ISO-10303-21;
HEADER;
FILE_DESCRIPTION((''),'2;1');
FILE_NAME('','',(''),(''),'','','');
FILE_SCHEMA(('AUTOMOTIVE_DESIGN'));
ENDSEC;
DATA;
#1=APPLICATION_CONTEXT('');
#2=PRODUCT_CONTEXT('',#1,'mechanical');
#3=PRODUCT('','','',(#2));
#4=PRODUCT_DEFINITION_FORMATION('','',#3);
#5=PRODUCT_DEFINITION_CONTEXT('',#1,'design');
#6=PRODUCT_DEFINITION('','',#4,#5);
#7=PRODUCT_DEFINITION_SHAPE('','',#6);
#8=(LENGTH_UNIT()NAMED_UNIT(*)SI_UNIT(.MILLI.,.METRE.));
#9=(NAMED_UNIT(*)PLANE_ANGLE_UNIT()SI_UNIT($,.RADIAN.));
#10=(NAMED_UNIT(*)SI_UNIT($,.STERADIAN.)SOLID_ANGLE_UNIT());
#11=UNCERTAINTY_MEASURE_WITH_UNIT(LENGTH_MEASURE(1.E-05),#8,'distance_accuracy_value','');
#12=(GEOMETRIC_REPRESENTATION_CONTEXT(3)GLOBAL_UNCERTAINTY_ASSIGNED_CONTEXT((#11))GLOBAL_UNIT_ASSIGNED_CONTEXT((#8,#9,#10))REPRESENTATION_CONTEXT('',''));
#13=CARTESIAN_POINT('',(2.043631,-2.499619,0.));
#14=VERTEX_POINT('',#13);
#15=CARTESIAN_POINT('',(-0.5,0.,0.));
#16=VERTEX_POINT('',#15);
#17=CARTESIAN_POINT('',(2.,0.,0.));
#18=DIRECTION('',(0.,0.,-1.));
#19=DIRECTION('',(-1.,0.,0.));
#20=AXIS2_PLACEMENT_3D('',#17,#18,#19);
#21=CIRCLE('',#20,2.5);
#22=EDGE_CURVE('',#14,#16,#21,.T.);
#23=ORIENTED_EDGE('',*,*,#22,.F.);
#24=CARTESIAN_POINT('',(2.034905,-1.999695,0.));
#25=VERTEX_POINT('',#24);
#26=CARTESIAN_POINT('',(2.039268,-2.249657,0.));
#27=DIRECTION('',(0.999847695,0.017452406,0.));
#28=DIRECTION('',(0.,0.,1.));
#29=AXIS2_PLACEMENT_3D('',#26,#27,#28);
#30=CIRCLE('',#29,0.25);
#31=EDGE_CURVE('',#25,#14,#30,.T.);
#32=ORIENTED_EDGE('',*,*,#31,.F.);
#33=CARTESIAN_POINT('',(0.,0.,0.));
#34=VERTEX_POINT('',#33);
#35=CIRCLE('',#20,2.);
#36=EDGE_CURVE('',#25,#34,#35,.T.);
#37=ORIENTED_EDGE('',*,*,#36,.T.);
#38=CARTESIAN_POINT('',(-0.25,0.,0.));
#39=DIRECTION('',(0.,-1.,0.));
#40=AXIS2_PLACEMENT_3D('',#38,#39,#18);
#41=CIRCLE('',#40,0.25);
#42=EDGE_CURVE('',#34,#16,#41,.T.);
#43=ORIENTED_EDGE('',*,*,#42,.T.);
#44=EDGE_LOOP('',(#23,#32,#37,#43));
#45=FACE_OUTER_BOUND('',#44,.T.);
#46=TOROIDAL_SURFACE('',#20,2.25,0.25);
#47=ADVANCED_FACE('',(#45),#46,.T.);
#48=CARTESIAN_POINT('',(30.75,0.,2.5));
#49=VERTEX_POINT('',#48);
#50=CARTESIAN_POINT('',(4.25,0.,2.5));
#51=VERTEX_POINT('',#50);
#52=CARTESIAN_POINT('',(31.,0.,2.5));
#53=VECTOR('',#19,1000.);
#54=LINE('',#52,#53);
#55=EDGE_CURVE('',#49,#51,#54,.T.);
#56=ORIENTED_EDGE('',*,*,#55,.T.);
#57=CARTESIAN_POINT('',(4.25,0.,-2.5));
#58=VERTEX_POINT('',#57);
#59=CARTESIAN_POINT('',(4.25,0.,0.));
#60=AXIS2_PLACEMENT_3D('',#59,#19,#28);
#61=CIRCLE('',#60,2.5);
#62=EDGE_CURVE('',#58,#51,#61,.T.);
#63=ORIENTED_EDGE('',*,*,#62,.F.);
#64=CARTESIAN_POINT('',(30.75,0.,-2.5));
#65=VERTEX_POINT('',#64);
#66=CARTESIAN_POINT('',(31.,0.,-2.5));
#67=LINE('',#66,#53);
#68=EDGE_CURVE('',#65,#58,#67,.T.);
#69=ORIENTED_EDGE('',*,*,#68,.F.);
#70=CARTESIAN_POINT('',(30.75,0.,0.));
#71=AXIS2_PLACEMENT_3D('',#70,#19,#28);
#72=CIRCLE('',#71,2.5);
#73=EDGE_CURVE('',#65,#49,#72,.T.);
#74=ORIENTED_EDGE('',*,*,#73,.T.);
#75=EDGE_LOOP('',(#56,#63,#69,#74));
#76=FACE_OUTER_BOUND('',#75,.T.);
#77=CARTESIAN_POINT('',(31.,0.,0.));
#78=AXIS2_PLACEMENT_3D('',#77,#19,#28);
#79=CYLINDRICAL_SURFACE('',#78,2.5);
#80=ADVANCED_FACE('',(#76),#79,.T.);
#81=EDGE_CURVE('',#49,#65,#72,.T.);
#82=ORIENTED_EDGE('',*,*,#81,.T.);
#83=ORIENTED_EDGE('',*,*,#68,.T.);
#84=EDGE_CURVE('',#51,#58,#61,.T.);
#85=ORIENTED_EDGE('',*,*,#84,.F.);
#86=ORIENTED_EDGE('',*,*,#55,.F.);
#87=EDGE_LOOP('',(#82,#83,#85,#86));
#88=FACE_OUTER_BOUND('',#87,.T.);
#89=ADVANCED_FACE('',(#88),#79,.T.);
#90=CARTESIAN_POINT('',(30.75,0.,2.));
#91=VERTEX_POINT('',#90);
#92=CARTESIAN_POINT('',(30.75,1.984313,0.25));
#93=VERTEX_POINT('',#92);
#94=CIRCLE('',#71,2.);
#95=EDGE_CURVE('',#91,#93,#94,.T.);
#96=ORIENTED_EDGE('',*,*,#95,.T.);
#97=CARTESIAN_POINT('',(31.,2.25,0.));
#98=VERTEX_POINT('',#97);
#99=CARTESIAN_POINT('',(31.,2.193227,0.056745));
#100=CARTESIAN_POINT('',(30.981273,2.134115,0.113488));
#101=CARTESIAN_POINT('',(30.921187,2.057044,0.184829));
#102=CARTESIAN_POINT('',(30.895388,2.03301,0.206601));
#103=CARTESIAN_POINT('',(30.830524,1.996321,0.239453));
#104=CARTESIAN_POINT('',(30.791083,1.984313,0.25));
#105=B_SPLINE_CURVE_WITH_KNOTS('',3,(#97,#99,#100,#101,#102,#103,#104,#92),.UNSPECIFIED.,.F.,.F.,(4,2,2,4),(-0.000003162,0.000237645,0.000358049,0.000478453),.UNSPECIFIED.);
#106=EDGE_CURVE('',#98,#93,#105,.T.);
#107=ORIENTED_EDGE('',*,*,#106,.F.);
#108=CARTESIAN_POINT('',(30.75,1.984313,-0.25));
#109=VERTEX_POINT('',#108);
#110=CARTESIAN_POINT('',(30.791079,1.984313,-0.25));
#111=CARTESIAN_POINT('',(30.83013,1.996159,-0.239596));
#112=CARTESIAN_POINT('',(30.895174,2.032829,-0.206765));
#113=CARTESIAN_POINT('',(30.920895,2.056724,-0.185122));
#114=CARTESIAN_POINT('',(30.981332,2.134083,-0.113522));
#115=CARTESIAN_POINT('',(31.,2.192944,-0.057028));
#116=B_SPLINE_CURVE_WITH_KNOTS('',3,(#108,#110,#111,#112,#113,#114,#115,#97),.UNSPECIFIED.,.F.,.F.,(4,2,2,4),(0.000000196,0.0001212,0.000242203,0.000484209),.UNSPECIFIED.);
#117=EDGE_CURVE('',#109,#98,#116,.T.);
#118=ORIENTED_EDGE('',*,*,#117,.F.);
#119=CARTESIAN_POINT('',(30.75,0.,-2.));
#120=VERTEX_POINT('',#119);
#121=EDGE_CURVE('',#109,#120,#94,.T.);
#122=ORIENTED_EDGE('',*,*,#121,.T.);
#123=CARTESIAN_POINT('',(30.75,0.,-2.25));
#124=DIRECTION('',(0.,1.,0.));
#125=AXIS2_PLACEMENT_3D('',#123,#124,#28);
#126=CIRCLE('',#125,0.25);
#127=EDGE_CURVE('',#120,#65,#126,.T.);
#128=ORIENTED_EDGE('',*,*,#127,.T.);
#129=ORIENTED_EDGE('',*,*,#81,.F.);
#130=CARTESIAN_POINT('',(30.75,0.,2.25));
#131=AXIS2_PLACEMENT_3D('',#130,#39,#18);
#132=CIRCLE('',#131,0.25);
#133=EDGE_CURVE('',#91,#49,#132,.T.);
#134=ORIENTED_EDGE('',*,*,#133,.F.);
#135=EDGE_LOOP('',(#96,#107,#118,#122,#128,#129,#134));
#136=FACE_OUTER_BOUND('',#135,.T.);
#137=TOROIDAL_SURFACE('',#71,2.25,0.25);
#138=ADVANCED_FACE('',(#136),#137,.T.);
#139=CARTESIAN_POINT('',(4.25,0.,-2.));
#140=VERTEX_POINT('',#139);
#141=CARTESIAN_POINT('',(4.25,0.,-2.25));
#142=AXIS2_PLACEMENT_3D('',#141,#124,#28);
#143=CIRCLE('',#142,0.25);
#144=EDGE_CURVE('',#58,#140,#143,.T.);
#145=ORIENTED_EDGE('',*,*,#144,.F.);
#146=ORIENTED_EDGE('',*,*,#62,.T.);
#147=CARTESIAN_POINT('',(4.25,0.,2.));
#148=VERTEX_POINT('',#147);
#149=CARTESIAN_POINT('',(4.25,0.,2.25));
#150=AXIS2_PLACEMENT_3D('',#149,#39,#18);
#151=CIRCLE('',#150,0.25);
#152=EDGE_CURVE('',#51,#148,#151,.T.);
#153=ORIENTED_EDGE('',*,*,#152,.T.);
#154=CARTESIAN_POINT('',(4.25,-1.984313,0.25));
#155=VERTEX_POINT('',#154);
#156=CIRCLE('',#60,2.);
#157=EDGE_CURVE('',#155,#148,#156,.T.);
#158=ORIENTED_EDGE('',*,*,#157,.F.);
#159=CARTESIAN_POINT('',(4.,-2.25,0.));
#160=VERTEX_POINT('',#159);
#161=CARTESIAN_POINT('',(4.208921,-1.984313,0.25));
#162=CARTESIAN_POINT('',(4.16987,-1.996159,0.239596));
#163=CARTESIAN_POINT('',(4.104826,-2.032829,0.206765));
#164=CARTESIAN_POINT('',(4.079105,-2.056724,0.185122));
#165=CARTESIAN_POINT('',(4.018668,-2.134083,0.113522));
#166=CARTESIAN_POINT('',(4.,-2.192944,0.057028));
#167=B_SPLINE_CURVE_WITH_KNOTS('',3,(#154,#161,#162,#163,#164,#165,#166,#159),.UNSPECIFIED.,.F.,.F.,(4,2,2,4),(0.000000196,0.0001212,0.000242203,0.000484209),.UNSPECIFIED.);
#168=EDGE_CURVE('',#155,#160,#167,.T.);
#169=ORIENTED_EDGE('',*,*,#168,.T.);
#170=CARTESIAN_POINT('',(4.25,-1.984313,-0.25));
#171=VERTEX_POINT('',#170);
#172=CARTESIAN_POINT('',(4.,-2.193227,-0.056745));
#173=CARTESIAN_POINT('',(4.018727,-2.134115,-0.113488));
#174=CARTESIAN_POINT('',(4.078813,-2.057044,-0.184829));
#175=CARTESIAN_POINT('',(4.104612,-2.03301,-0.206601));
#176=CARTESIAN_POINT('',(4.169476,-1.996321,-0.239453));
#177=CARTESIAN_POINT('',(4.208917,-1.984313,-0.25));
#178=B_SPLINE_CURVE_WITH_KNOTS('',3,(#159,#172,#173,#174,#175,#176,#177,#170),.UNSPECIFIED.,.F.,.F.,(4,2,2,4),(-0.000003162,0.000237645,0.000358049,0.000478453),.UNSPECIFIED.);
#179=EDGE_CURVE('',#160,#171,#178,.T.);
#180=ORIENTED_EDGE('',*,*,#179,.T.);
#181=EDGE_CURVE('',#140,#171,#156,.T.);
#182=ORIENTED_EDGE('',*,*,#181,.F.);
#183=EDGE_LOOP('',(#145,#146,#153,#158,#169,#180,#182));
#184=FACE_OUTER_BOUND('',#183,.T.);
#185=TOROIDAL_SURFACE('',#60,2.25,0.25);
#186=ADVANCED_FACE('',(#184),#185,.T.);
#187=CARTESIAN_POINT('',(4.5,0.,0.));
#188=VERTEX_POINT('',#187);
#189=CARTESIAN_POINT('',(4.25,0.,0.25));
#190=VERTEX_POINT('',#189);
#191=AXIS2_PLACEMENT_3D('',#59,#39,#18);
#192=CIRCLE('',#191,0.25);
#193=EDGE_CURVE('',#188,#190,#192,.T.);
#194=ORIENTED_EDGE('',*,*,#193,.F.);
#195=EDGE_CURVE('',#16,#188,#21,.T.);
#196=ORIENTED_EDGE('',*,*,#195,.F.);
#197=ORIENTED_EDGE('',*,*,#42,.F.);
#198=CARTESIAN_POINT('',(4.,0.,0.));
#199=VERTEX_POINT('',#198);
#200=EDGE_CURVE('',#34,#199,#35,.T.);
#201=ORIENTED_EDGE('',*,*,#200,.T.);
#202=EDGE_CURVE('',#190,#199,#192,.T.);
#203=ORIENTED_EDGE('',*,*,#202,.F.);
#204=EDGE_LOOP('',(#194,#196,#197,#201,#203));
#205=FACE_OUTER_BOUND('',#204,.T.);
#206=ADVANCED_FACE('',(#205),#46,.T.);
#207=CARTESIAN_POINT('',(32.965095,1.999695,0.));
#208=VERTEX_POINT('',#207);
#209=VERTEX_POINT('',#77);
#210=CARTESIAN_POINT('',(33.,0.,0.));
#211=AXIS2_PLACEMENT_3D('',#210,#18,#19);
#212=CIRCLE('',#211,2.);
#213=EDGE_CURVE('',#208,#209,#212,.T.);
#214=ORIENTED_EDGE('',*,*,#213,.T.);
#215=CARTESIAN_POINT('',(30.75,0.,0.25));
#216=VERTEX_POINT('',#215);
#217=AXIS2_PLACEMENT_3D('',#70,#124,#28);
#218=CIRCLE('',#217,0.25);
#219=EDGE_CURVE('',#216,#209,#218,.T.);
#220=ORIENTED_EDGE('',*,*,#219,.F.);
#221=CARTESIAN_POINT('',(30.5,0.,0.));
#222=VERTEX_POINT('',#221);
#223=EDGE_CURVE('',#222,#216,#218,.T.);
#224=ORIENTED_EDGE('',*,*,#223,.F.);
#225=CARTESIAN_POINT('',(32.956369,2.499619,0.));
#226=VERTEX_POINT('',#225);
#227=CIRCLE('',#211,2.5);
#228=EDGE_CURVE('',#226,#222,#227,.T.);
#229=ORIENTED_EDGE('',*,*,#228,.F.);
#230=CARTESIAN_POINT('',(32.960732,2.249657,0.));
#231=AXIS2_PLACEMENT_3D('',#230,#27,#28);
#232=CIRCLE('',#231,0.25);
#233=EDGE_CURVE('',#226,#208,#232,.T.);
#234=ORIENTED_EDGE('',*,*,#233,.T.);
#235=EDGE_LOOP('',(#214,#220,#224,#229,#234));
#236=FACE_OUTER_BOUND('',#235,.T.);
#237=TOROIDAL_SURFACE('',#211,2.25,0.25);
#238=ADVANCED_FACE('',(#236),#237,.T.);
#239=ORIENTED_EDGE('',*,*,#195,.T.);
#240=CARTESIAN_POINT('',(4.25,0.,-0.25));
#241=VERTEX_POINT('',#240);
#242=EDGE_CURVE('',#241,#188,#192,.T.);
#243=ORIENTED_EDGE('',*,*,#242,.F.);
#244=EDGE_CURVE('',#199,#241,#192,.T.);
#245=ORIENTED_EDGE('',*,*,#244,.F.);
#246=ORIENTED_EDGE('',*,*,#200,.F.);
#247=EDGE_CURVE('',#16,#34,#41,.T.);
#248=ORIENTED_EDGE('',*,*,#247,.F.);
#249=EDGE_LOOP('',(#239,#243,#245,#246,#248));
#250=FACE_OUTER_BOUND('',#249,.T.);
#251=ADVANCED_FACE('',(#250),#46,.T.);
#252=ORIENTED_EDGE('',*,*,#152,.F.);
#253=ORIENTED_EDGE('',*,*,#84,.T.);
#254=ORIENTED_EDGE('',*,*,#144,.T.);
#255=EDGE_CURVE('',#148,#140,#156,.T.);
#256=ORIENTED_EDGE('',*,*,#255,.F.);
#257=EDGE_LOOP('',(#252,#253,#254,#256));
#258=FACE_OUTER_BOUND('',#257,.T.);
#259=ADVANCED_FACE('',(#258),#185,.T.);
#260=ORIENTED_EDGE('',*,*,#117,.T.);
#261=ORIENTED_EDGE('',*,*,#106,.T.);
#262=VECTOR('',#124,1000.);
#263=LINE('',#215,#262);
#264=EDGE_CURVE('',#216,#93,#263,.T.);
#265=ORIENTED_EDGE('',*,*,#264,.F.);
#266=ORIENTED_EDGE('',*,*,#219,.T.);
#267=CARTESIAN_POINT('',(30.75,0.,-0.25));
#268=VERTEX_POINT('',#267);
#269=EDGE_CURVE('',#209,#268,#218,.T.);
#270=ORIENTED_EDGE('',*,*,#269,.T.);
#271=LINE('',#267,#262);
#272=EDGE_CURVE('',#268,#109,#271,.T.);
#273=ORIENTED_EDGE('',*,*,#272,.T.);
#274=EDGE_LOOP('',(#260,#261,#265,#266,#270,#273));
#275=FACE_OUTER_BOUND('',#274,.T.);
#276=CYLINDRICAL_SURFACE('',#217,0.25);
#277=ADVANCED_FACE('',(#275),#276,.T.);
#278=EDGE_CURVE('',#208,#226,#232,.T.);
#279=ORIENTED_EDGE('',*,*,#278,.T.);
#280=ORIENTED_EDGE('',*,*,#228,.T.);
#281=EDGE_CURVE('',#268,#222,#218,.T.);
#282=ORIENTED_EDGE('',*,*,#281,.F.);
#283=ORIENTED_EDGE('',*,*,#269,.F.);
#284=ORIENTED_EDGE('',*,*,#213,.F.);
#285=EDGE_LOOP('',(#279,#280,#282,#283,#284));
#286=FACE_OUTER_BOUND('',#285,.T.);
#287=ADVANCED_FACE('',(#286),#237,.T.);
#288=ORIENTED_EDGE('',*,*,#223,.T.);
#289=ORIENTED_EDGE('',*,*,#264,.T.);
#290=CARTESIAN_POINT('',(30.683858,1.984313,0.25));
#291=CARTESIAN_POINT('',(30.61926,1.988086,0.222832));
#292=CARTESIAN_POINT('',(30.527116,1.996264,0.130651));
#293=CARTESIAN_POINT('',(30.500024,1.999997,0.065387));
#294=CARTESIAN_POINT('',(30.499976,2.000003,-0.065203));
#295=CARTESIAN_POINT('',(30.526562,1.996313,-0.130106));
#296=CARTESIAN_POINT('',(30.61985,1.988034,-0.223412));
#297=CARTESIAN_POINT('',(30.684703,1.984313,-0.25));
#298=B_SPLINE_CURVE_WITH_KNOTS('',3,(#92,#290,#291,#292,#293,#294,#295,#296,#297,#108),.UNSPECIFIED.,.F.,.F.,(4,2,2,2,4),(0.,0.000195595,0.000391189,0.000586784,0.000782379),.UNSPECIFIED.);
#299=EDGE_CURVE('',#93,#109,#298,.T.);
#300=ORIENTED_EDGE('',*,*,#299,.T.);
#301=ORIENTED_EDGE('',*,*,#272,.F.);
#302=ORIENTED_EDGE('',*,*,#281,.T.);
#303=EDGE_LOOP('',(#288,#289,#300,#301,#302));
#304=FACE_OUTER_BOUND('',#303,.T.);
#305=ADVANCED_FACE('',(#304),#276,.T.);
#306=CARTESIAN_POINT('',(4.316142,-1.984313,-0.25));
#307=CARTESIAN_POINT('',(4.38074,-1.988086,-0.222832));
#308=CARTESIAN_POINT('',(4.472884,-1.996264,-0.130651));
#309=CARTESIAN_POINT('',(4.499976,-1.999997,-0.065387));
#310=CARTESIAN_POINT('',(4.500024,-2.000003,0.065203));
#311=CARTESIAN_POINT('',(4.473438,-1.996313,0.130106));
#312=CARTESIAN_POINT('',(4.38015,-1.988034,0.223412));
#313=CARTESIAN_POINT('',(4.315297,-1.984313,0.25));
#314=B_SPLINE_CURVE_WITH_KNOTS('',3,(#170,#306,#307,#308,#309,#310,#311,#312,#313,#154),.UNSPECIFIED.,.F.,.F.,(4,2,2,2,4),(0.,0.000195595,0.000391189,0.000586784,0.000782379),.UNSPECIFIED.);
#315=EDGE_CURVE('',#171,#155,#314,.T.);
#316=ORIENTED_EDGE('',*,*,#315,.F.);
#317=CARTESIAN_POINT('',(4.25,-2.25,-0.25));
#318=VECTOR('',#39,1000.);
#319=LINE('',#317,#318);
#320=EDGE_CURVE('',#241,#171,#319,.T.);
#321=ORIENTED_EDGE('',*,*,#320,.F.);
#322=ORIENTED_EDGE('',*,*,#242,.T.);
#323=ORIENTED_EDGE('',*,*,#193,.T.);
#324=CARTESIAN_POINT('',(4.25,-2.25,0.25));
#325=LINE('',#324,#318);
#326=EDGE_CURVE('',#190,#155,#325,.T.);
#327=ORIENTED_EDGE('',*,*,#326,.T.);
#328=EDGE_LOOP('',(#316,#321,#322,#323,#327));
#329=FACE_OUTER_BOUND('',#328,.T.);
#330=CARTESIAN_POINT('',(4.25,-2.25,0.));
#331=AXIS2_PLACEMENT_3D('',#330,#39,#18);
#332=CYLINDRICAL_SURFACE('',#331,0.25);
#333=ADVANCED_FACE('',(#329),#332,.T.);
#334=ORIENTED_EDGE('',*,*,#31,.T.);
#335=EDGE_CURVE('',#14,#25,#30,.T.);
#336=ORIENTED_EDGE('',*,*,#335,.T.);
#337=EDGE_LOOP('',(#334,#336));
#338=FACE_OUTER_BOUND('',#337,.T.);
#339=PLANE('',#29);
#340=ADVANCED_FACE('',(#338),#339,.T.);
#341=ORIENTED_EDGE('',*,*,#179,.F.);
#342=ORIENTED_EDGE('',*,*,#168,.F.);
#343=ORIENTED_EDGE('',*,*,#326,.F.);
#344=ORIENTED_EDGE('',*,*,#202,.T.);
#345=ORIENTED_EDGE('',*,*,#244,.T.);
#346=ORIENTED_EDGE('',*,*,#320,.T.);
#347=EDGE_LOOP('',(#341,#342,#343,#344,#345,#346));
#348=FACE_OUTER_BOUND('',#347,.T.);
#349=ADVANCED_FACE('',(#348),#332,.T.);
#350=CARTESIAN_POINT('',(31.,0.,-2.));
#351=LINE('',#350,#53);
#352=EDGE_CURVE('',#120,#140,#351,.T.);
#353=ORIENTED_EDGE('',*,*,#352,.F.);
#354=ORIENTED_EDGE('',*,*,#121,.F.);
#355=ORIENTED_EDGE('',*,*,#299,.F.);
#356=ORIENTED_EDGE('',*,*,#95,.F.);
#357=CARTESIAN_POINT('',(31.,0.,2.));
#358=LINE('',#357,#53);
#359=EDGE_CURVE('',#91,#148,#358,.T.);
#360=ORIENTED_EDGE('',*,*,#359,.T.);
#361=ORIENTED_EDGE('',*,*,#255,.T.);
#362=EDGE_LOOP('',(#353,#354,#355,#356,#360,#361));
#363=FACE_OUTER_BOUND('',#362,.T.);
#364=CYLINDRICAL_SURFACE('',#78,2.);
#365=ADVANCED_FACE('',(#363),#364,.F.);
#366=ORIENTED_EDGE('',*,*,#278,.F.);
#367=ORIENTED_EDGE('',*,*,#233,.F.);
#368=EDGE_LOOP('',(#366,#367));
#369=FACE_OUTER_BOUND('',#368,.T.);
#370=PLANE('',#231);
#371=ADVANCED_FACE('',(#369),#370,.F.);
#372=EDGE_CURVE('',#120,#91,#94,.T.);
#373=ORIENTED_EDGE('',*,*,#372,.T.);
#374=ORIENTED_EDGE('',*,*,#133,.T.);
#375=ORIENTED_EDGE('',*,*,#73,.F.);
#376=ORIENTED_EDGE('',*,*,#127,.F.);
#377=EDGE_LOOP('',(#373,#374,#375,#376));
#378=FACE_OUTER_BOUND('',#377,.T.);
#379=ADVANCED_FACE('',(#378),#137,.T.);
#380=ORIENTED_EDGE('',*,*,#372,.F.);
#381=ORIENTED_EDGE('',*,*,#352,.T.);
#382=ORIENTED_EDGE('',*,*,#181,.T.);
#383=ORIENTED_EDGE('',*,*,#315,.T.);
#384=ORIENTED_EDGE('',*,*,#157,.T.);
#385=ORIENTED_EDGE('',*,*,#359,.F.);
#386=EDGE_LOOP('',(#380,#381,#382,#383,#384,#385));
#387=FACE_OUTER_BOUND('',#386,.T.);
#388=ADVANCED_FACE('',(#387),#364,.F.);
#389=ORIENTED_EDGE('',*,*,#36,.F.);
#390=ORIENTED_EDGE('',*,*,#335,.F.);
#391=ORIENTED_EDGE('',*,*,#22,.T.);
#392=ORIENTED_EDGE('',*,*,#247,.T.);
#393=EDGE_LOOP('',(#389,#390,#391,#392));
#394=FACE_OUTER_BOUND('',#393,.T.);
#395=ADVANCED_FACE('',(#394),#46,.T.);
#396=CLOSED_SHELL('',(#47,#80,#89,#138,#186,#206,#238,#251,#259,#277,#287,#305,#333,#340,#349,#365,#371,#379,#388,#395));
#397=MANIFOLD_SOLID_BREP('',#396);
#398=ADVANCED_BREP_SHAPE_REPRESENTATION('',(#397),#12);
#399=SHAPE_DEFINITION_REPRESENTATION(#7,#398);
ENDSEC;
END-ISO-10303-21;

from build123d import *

# Parameters (mm, degrees)
SKETCH2_W      = 0.25
SKETCH2_H      = 2.25
SKETCH3_R      = 0.25
REVOLVE3_ANGLE = 271
SKETCH4_W      = 0.25
SKETCH4_H      = 2.25
SKETCH5_R      = 0.25
REVOLVE5_ANGLE = 271


with BuildPart() as part:
    # Sketch1 → Revolve1 (revolve)
    with BuildSketch(Plane.XY, mode=Mode.PRIVATE) as revolve1_sk:
        with BuildLine():
            Line((4.25, 2), (30.75, 2))
            ThreePointArc((30.75, 2), (31, 2.25), (30.75, 2.5))
            Line((30.75, 2.5), (4.25, 2.5))
            ThreePointArc((4.25, 2.5), (4, 2.25), (4.25, 2))
        make_face()
    revolve(revolve1_sk.sketch.rotate(Axis((31, 0, 0), (-1, 0, 0)), 270), axis=Axis((31, 0, 0), (-1, 0, 0)))

    # Sketch2 → Revolve2 (revolve)
    with BuildSketch(Plane.XY, mode=Mode.PRIVATE) as revolve2_sk:
        with Locations((30.875, 1.125)):
            Rectangle(SKETCH2_W, SKETCH2_H)
    revolve(revolve2_sk.sketch.rotate(Axis((30.75, 0, 0), (0, 1, 0)), 270), axis=Axis((30.75, 0, 0), (0, 1, 0)))

    # Sketch3 → Revolve3 (revolve)
    with BuildSketch(Plane(origin=(0, 0, 0), x_dir=(1, 0, 0), z_dir=(0, 1, 0))):
        with Locations(Location((30.75, 0, 0), (0, 0, 269.999999944))):
            Circle(SKETCH3_R)
    revolve(axis=Axis((33, 0, -2.5), (0, 0, 1)), revolution_arc=REVOLVE3_ANGLE)

    # Sketch4 → Revolve4 (revolve)
    with BuildSketch(Plane.XY, mode=Mode.PRIVATE) as revolve4_sk:
        with Locations((4.375, -1.125)):
            Rectangle(SKETCH4_W, SKETCH4_H)
    revolve(revolve4_sk.sketch.rotate(Axis((4.25, -2.25, 0), (0, 1, 0)), 90), axis=Axis((4.25, -2.25, 0), (0, 1, 0)))

    # Sketch5 → Revolve5 (revolve)
    with BuildSketch(Plane(origin=(0, 0, 0), x_dir=(1, 0, 0), z_dir=(0, 1, 0))):
        with Locations(Location((4.25, 0, 0), (0, 0, 90))):
            Circle(SKETCH5_R)
    revolve(axis=Axis((2, 0, 2.5), (0, 0, 1)), revolution_arc=REVOLVE5_ANGLE)


solid = part.part
